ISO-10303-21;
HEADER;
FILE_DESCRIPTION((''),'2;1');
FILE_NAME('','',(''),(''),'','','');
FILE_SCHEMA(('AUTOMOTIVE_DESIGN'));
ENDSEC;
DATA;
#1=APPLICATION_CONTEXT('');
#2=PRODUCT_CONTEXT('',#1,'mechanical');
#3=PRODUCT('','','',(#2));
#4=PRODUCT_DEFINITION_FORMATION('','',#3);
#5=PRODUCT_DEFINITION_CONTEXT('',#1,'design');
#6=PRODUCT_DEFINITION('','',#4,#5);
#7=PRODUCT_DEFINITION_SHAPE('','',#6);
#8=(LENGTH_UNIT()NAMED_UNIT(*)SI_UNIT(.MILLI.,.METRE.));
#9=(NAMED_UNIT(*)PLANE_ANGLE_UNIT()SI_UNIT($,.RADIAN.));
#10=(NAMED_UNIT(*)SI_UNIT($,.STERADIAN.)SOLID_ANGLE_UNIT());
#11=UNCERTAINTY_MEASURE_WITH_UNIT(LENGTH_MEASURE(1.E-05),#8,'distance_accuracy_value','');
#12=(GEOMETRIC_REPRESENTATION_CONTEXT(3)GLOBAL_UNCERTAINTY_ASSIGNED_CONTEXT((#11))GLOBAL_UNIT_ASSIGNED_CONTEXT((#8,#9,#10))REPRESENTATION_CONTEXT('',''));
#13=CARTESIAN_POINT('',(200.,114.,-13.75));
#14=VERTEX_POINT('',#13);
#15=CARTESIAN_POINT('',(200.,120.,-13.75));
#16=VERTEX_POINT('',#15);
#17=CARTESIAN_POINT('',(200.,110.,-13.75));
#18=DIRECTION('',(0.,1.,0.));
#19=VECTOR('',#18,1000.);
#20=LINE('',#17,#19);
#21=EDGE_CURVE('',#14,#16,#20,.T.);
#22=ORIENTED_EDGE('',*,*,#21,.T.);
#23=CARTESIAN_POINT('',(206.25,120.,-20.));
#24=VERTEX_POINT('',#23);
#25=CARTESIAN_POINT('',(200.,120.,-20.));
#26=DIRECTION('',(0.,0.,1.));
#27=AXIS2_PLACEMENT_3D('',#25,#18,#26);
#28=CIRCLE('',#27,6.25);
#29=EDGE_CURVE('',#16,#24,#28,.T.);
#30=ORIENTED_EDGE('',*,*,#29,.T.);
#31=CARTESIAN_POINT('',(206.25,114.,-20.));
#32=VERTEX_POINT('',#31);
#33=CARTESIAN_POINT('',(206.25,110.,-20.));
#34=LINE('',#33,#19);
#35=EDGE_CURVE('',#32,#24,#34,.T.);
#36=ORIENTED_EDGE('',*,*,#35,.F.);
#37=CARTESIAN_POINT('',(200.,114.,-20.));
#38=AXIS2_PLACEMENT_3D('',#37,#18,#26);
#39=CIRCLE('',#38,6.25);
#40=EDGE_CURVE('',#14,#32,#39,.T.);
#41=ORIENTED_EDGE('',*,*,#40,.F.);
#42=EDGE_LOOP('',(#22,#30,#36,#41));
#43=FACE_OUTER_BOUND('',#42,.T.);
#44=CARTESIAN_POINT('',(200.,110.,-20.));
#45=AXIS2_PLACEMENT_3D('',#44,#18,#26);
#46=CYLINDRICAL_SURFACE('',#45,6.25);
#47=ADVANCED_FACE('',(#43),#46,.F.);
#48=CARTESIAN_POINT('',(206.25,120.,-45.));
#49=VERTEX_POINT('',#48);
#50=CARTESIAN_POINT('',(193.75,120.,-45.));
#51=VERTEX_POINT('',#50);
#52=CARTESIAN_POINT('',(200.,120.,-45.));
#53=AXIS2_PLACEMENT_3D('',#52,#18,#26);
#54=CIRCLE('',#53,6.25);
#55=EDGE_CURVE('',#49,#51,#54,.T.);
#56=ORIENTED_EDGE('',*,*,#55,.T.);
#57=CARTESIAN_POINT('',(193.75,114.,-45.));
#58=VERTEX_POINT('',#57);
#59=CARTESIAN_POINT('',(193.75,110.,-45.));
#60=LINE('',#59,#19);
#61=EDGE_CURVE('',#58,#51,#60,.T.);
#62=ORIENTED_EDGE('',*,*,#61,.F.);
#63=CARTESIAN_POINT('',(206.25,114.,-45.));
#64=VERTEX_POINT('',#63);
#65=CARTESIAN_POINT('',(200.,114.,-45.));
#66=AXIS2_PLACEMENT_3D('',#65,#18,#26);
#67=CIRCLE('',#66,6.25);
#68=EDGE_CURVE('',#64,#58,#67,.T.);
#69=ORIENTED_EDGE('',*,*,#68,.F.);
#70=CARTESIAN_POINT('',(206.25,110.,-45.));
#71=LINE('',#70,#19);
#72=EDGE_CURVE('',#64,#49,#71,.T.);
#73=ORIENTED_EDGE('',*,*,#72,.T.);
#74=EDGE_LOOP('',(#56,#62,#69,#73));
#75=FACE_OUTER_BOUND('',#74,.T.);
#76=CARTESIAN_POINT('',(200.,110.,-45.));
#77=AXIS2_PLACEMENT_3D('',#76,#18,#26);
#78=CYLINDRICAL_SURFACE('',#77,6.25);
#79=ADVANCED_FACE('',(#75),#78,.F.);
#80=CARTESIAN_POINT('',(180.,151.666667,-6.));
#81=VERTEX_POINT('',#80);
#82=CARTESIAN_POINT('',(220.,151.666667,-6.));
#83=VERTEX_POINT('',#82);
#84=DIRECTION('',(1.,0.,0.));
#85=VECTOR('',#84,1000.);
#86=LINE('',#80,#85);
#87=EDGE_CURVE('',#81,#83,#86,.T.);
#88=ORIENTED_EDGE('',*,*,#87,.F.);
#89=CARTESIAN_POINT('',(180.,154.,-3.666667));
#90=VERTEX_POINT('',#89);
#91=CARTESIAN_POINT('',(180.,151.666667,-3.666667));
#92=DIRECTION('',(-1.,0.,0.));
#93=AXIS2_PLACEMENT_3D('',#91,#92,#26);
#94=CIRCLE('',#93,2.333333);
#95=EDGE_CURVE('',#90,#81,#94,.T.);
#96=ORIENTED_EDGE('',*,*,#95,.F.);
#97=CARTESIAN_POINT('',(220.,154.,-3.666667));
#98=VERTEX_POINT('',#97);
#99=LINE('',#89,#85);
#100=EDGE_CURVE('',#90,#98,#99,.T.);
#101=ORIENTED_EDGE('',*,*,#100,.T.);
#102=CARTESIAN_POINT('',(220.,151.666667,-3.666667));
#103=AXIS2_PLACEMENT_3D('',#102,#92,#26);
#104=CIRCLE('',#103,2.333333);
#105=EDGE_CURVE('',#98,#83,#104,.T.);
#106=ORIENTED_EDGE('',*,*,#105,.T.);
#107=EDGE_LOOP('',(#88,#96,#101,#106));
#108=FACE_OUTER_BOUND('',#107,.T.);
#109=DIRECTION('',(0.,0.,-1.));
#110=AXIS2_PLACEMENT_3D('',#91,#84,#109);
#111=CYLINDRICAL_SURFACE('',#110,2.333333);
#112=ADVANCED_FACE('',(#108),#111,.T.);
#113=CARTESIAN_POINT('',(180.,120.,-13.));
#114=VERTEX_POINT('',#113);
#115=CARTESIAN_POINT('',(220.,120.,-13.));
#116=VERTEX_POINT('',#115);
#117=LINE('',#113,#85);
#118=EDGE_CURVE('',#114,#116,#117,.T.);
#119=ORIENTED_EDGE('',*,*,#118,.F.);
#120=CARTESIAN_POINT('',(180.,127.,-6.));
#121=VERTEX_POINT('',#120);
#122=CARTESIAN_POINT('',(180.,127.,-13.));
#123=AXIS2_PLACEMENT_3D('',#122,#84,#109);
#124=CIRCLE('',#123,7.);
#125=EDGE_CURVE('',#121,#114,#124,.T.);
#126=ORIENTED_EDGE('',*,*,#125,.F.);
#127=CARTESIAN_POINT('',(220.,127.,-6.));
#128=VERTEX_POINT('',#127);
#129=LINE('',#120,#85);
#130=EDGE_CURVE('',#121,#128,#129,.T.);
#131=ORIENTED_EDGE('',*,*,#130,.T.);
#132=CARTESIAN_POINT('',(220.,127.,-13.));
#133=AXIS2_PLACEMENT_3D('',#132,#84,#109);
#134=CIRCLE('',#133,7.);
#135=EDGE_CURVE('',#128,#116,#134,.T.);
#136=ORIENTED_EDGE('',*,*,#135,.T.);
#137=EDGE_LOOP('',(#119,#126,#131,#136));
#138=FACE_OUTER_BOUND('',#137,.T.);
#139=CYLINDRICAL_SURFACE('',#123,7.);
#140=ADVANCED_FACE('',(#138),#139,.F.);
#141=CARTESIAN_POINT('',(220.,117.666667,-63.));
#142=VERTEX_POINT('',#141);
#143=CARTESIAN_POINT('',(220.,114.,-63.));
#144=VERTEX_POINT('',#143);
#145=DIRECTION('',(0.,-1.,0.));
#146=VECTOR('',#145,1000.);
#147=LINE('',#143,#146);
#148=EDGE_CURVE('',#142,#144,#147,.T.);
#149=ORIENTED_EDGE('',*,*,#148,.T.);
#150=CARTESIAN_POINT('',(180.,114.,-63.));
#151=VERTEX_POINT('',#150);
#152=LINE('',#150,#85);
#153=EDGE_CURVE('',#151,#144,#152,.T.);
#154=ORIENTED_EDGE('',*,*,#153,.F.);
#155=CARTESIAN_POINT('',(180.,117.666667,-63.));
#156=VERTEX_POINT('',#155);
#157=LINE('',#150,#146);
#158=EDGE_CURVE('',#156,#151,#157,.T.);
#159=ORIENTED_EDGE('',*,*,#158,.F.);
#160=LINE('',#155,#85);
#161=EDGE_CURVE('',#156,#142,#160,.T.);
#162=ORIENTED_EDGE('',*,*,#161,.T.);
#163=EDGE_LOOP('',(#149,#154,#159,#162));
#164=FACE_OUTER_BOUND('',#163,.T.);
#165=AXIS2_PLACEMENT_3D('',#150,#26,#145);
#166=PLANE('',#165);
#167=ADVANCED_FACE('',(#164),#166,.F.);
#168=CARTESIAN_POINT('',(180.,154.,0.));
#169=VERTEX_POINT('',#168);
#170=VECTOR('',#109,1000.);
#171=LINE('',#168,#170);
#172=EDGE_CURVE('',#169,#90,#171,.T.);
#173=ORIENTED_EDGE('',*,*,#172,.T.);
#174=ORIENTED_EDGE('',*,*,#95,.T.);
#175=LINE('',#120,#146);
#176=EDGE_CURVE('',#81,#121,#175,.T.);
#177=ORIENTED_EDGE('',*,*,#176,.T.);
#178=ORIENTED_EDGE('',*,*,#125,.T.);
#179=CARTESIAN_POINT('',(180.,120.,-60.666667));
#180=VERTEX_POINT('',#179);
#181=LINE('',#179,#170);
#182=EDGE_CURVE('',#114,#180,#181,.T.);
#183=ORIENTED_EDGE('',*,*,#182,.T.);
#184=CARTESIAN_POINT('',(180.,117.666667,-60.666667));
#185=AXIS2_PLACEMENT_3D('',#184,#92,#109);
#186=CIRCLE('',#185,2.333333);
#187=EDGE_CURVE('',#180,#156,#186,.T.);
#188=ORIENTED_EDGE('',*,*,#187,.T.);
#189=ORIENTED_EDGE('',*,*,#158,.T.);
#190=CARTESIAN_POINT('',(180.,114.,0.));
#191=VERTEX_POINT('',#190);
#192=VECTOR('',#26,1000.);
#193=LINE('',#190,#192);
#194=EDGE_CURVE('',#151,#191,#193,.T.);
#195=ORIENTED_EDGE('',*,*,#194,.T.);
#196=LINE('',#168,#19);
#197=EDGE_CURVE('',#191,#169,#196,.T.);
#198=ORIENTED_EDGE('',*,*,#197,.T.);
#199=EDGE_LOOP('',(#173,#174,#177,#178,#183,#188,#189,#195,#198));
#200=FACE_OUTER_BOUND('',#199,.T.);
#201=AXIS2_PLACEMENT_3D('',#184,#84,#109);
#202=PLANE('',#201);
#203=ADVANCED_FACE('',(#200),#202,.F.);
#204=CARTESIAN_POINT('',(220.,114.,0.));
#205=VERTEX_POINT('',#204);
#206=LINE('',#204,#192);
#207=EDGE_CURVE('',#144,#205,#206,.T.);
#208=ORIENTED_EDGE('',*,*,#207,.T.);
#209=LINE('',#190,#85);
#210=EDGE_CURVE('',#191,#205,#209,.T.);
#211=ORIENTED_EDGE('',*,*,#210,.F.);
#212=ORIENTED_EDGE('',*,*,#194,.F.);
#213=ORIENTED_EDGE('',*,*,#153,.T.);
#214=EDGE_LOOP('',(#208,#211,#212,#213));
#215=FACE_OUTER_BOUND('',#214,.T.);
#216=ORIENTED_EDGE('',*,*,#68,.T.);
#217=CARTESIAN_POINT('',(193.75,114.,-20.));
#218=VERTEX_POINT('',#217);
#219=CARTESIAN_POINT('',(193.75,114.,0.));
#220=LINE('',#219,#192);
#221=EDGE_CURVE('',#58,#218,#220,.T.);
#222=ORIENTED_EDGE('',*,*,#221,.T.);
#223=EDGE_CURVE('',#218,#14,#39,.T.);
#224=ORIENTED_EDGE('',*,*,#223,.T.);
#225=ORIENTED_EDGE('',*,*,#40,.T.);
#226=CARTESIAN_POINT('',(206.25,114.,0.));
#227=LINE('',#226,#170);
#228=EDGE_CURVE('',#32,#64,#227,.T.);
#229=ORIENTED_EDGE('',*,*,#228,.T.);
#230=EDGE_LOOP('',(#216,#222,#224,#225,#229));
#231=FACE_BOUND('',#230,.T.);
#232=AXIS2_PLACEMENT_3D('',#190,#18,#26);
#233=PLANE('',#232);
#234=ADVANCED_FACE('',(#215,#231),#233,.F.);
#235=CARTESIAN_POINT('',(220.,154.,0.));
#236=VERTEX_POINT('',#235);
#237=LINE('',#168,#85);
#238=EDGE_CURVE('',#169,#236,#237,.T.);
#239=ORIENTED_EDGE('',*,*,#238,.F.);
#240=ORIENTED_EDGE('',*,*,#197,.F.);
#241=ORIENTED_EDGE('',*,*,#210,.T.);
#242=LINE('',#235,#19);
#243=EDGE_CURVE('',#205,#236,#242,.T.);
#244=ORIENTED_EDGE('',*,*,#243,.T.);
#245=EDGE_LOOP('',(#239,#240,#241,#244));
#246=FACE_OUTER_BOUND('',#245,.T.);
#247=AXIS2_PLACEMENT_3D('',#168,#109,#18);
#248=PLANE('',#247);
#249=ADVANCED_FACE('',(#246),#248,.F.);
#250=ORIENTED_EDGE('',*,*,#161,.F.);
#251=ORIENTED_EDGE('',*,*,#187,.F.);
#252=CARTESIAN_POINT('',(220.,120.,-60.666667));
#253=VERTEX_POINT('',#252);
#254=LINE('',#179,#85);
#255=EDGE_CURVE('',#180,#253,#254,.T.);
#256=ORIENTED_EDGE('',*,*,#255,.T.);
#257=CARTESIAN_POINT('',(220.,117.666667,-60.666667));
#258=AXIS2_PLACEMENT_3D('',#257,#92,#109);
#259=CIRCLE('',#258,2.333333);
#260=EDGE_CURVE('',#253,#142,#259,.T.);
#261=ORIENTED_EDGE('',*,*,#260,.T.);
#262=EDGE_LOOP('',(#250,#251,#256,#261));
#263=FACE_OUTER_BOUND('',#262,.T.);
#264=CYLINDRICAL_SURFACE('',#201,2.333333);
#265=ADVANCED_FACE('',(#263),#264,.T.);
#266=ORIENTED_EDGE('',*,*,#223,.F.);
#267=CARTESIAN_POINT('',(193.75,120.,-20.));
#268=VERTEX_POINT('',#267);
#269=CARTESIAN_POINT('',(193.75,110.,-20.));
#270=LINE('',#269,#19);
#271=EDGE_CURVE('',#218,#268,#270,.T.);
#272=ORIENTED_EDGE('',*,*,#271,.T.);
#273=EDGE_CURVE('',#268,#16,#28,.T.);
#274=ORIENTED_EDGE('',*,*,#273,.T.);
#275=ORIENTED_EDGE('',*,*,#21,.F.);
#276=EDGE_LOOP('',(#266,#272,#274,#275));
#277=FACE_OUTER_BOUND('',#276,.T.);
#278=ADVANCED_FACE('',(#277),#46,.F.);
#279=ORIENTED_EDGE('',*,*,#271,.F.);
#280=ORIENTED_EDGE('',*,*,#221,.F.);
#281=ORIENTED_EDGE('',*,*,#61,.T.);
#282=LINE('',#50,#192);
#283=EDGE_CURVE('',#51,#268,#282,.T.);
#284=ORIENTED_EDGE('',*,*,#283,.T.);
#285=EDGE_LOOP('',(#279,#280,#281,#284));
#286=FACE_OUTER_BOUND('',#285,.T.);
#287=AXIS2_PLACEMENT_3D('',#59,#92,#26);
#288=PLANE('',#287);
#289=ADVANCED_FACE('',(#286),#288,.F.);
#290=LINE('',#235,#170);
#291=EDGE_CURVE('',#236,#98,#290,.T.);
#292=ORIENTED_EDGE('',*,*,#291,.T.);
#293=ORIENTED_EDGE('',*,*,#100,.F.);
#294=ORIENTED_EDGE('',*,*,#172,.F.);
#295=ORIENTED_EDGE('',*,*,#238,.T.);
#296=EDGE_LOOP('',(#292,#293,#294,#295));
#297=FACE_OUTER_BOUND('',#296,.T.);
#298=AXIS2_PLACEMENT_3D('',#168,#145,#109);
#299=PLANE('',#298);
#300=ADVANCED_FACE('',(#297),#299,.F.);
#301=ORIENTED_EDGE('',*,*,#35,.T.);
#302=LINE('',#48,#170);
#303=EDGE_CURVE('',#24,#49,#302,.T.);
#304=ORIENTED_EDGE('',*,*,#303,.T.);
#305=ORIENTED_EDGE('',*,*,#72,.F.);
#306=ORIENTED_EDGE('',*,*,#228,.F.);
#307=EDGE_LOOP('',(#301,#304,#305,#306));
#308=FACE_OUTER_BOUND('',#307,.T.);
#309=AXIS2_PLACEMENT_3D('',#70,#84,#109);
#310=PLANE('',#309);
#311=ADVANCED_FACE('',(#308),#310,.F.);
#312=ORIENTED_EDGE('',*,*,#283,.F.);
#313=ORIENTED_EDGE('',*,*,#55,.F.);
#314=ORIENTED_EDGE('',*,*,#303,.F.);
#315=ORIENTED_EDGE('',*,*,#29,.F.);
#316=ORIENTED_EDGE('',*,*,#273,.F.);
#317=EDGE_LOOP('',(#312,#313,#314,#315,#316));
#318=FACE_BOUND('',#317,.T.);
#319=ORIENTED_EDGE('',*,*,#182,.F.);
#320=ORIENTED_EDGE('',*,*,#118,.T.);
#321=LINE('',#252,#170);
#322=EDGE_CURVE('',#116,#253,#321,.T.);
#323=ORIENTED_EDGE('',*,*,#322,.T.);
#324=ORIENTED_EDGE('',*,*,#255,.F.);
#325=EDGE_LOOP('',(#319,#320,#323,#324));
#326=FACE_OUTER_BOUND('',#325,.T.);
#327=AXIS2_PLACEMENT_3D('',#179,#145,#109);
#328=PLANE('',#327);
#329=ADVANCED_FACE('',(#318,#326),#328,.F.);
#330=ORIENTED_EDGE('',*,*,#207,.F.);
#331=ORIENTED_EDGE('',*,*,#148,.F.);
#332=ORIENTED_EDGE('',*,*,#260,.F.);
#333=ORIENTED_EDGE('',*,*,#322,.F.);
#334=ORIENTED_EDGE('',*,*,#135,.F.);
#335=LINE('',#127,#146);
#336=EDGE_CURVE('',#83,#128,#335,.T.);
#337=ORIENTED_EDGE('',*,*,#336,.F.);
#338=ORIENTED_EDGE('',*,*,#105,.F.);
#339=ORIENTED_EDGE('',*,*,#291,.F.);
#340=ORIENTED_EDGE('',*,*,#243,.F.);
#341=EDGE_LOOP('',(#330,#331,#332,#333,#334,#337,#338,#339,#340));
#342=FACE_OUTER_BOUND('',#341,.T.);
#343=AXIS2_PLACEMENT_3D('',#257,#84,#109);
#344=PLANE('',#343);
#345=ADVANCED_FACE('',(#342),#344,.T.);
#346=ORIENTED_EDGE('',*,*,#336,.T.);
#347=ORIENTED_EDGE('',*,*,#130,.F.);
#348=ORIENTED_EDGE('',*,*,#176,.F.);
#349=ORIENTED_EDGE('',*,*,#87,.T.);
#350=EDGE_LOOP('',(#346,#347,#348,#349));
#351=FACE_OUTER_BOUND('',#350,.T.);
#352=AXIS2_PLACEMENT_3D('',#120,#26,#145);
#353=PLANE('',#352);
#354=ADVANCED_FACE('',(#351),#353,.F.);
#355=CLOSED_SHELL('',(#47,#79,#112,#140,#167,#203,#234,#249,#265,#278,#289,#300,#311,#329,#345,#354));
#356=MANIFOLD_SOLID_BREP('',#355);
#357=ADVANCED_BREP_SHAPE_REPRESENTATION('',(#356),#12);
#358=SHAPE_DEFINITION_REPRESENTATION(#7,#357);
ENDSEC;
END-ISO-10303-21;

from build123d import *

# Parameters (mm, degrees)
HOT_ROLLED_UNEQUAL_ANGLE_GB_T_706_2008_6_DEPTH = 40
CUT_EXTRUDE1_DEPTH                             = 10


with BuildPart() as part:
    # Sketch1 → Hot-rolled unequal angle GB∕T 706-2008 63 X 40 X 6 (1) (new body)
    with BuildSketch(Plane(origin=(220, 114, 0), x_dir=(0, 1, 0), z_dir=(-1, 0, 0))):
        with BuildLine():
            Line((0, 0), (0, 63))
            Line((0, 63), (3.666666667, 63))
            ThreePointArc((3.666666667, 63), (5.316582489, 62.316582489), (6, 60.666666667))
            Line((6, 60.666666667), (6, 13))
            ThreePointArc((6, 13), (8.050252532, 8.050252532), (13, 6))
            Line((13, 6), (37.666666667, 6))
            ThreePointArc((37.666666667, 6), (39.316582489, 5.316582489), (40, 3.666666667))
            Line((40, 3.666666667), (40, 0))
            Line((40, 0), (0, 0))
        make_face()
    extrude(amount=HOT_ROLLED_UNEQUAL_ANGLE_GB_T_706_2008_6_DEPTH)

    # Sketch2 → Cut-Extrude1 (cut)
    with BuildSketch(Plane(origin=(0, 120, 0), x_dir=(1, 0, 0), z_dir=(0, 1, 0))):
        with BuildLine():
            Line((206.25, 45), (206.25, 20))
            ThreePointArc((206.25, 20), (200, 13.75), (193.75, 20))
            Line((193.75, 20), (193.75, 45))
            ThreePointArc((193.75, 45), (200, 51.25), (206.25, 45))
        make_face()
    extrude(amount=-CUT_EXTRUDE1_DEPTH, mode=Mode.SUBTRACT)


solid = part.part
